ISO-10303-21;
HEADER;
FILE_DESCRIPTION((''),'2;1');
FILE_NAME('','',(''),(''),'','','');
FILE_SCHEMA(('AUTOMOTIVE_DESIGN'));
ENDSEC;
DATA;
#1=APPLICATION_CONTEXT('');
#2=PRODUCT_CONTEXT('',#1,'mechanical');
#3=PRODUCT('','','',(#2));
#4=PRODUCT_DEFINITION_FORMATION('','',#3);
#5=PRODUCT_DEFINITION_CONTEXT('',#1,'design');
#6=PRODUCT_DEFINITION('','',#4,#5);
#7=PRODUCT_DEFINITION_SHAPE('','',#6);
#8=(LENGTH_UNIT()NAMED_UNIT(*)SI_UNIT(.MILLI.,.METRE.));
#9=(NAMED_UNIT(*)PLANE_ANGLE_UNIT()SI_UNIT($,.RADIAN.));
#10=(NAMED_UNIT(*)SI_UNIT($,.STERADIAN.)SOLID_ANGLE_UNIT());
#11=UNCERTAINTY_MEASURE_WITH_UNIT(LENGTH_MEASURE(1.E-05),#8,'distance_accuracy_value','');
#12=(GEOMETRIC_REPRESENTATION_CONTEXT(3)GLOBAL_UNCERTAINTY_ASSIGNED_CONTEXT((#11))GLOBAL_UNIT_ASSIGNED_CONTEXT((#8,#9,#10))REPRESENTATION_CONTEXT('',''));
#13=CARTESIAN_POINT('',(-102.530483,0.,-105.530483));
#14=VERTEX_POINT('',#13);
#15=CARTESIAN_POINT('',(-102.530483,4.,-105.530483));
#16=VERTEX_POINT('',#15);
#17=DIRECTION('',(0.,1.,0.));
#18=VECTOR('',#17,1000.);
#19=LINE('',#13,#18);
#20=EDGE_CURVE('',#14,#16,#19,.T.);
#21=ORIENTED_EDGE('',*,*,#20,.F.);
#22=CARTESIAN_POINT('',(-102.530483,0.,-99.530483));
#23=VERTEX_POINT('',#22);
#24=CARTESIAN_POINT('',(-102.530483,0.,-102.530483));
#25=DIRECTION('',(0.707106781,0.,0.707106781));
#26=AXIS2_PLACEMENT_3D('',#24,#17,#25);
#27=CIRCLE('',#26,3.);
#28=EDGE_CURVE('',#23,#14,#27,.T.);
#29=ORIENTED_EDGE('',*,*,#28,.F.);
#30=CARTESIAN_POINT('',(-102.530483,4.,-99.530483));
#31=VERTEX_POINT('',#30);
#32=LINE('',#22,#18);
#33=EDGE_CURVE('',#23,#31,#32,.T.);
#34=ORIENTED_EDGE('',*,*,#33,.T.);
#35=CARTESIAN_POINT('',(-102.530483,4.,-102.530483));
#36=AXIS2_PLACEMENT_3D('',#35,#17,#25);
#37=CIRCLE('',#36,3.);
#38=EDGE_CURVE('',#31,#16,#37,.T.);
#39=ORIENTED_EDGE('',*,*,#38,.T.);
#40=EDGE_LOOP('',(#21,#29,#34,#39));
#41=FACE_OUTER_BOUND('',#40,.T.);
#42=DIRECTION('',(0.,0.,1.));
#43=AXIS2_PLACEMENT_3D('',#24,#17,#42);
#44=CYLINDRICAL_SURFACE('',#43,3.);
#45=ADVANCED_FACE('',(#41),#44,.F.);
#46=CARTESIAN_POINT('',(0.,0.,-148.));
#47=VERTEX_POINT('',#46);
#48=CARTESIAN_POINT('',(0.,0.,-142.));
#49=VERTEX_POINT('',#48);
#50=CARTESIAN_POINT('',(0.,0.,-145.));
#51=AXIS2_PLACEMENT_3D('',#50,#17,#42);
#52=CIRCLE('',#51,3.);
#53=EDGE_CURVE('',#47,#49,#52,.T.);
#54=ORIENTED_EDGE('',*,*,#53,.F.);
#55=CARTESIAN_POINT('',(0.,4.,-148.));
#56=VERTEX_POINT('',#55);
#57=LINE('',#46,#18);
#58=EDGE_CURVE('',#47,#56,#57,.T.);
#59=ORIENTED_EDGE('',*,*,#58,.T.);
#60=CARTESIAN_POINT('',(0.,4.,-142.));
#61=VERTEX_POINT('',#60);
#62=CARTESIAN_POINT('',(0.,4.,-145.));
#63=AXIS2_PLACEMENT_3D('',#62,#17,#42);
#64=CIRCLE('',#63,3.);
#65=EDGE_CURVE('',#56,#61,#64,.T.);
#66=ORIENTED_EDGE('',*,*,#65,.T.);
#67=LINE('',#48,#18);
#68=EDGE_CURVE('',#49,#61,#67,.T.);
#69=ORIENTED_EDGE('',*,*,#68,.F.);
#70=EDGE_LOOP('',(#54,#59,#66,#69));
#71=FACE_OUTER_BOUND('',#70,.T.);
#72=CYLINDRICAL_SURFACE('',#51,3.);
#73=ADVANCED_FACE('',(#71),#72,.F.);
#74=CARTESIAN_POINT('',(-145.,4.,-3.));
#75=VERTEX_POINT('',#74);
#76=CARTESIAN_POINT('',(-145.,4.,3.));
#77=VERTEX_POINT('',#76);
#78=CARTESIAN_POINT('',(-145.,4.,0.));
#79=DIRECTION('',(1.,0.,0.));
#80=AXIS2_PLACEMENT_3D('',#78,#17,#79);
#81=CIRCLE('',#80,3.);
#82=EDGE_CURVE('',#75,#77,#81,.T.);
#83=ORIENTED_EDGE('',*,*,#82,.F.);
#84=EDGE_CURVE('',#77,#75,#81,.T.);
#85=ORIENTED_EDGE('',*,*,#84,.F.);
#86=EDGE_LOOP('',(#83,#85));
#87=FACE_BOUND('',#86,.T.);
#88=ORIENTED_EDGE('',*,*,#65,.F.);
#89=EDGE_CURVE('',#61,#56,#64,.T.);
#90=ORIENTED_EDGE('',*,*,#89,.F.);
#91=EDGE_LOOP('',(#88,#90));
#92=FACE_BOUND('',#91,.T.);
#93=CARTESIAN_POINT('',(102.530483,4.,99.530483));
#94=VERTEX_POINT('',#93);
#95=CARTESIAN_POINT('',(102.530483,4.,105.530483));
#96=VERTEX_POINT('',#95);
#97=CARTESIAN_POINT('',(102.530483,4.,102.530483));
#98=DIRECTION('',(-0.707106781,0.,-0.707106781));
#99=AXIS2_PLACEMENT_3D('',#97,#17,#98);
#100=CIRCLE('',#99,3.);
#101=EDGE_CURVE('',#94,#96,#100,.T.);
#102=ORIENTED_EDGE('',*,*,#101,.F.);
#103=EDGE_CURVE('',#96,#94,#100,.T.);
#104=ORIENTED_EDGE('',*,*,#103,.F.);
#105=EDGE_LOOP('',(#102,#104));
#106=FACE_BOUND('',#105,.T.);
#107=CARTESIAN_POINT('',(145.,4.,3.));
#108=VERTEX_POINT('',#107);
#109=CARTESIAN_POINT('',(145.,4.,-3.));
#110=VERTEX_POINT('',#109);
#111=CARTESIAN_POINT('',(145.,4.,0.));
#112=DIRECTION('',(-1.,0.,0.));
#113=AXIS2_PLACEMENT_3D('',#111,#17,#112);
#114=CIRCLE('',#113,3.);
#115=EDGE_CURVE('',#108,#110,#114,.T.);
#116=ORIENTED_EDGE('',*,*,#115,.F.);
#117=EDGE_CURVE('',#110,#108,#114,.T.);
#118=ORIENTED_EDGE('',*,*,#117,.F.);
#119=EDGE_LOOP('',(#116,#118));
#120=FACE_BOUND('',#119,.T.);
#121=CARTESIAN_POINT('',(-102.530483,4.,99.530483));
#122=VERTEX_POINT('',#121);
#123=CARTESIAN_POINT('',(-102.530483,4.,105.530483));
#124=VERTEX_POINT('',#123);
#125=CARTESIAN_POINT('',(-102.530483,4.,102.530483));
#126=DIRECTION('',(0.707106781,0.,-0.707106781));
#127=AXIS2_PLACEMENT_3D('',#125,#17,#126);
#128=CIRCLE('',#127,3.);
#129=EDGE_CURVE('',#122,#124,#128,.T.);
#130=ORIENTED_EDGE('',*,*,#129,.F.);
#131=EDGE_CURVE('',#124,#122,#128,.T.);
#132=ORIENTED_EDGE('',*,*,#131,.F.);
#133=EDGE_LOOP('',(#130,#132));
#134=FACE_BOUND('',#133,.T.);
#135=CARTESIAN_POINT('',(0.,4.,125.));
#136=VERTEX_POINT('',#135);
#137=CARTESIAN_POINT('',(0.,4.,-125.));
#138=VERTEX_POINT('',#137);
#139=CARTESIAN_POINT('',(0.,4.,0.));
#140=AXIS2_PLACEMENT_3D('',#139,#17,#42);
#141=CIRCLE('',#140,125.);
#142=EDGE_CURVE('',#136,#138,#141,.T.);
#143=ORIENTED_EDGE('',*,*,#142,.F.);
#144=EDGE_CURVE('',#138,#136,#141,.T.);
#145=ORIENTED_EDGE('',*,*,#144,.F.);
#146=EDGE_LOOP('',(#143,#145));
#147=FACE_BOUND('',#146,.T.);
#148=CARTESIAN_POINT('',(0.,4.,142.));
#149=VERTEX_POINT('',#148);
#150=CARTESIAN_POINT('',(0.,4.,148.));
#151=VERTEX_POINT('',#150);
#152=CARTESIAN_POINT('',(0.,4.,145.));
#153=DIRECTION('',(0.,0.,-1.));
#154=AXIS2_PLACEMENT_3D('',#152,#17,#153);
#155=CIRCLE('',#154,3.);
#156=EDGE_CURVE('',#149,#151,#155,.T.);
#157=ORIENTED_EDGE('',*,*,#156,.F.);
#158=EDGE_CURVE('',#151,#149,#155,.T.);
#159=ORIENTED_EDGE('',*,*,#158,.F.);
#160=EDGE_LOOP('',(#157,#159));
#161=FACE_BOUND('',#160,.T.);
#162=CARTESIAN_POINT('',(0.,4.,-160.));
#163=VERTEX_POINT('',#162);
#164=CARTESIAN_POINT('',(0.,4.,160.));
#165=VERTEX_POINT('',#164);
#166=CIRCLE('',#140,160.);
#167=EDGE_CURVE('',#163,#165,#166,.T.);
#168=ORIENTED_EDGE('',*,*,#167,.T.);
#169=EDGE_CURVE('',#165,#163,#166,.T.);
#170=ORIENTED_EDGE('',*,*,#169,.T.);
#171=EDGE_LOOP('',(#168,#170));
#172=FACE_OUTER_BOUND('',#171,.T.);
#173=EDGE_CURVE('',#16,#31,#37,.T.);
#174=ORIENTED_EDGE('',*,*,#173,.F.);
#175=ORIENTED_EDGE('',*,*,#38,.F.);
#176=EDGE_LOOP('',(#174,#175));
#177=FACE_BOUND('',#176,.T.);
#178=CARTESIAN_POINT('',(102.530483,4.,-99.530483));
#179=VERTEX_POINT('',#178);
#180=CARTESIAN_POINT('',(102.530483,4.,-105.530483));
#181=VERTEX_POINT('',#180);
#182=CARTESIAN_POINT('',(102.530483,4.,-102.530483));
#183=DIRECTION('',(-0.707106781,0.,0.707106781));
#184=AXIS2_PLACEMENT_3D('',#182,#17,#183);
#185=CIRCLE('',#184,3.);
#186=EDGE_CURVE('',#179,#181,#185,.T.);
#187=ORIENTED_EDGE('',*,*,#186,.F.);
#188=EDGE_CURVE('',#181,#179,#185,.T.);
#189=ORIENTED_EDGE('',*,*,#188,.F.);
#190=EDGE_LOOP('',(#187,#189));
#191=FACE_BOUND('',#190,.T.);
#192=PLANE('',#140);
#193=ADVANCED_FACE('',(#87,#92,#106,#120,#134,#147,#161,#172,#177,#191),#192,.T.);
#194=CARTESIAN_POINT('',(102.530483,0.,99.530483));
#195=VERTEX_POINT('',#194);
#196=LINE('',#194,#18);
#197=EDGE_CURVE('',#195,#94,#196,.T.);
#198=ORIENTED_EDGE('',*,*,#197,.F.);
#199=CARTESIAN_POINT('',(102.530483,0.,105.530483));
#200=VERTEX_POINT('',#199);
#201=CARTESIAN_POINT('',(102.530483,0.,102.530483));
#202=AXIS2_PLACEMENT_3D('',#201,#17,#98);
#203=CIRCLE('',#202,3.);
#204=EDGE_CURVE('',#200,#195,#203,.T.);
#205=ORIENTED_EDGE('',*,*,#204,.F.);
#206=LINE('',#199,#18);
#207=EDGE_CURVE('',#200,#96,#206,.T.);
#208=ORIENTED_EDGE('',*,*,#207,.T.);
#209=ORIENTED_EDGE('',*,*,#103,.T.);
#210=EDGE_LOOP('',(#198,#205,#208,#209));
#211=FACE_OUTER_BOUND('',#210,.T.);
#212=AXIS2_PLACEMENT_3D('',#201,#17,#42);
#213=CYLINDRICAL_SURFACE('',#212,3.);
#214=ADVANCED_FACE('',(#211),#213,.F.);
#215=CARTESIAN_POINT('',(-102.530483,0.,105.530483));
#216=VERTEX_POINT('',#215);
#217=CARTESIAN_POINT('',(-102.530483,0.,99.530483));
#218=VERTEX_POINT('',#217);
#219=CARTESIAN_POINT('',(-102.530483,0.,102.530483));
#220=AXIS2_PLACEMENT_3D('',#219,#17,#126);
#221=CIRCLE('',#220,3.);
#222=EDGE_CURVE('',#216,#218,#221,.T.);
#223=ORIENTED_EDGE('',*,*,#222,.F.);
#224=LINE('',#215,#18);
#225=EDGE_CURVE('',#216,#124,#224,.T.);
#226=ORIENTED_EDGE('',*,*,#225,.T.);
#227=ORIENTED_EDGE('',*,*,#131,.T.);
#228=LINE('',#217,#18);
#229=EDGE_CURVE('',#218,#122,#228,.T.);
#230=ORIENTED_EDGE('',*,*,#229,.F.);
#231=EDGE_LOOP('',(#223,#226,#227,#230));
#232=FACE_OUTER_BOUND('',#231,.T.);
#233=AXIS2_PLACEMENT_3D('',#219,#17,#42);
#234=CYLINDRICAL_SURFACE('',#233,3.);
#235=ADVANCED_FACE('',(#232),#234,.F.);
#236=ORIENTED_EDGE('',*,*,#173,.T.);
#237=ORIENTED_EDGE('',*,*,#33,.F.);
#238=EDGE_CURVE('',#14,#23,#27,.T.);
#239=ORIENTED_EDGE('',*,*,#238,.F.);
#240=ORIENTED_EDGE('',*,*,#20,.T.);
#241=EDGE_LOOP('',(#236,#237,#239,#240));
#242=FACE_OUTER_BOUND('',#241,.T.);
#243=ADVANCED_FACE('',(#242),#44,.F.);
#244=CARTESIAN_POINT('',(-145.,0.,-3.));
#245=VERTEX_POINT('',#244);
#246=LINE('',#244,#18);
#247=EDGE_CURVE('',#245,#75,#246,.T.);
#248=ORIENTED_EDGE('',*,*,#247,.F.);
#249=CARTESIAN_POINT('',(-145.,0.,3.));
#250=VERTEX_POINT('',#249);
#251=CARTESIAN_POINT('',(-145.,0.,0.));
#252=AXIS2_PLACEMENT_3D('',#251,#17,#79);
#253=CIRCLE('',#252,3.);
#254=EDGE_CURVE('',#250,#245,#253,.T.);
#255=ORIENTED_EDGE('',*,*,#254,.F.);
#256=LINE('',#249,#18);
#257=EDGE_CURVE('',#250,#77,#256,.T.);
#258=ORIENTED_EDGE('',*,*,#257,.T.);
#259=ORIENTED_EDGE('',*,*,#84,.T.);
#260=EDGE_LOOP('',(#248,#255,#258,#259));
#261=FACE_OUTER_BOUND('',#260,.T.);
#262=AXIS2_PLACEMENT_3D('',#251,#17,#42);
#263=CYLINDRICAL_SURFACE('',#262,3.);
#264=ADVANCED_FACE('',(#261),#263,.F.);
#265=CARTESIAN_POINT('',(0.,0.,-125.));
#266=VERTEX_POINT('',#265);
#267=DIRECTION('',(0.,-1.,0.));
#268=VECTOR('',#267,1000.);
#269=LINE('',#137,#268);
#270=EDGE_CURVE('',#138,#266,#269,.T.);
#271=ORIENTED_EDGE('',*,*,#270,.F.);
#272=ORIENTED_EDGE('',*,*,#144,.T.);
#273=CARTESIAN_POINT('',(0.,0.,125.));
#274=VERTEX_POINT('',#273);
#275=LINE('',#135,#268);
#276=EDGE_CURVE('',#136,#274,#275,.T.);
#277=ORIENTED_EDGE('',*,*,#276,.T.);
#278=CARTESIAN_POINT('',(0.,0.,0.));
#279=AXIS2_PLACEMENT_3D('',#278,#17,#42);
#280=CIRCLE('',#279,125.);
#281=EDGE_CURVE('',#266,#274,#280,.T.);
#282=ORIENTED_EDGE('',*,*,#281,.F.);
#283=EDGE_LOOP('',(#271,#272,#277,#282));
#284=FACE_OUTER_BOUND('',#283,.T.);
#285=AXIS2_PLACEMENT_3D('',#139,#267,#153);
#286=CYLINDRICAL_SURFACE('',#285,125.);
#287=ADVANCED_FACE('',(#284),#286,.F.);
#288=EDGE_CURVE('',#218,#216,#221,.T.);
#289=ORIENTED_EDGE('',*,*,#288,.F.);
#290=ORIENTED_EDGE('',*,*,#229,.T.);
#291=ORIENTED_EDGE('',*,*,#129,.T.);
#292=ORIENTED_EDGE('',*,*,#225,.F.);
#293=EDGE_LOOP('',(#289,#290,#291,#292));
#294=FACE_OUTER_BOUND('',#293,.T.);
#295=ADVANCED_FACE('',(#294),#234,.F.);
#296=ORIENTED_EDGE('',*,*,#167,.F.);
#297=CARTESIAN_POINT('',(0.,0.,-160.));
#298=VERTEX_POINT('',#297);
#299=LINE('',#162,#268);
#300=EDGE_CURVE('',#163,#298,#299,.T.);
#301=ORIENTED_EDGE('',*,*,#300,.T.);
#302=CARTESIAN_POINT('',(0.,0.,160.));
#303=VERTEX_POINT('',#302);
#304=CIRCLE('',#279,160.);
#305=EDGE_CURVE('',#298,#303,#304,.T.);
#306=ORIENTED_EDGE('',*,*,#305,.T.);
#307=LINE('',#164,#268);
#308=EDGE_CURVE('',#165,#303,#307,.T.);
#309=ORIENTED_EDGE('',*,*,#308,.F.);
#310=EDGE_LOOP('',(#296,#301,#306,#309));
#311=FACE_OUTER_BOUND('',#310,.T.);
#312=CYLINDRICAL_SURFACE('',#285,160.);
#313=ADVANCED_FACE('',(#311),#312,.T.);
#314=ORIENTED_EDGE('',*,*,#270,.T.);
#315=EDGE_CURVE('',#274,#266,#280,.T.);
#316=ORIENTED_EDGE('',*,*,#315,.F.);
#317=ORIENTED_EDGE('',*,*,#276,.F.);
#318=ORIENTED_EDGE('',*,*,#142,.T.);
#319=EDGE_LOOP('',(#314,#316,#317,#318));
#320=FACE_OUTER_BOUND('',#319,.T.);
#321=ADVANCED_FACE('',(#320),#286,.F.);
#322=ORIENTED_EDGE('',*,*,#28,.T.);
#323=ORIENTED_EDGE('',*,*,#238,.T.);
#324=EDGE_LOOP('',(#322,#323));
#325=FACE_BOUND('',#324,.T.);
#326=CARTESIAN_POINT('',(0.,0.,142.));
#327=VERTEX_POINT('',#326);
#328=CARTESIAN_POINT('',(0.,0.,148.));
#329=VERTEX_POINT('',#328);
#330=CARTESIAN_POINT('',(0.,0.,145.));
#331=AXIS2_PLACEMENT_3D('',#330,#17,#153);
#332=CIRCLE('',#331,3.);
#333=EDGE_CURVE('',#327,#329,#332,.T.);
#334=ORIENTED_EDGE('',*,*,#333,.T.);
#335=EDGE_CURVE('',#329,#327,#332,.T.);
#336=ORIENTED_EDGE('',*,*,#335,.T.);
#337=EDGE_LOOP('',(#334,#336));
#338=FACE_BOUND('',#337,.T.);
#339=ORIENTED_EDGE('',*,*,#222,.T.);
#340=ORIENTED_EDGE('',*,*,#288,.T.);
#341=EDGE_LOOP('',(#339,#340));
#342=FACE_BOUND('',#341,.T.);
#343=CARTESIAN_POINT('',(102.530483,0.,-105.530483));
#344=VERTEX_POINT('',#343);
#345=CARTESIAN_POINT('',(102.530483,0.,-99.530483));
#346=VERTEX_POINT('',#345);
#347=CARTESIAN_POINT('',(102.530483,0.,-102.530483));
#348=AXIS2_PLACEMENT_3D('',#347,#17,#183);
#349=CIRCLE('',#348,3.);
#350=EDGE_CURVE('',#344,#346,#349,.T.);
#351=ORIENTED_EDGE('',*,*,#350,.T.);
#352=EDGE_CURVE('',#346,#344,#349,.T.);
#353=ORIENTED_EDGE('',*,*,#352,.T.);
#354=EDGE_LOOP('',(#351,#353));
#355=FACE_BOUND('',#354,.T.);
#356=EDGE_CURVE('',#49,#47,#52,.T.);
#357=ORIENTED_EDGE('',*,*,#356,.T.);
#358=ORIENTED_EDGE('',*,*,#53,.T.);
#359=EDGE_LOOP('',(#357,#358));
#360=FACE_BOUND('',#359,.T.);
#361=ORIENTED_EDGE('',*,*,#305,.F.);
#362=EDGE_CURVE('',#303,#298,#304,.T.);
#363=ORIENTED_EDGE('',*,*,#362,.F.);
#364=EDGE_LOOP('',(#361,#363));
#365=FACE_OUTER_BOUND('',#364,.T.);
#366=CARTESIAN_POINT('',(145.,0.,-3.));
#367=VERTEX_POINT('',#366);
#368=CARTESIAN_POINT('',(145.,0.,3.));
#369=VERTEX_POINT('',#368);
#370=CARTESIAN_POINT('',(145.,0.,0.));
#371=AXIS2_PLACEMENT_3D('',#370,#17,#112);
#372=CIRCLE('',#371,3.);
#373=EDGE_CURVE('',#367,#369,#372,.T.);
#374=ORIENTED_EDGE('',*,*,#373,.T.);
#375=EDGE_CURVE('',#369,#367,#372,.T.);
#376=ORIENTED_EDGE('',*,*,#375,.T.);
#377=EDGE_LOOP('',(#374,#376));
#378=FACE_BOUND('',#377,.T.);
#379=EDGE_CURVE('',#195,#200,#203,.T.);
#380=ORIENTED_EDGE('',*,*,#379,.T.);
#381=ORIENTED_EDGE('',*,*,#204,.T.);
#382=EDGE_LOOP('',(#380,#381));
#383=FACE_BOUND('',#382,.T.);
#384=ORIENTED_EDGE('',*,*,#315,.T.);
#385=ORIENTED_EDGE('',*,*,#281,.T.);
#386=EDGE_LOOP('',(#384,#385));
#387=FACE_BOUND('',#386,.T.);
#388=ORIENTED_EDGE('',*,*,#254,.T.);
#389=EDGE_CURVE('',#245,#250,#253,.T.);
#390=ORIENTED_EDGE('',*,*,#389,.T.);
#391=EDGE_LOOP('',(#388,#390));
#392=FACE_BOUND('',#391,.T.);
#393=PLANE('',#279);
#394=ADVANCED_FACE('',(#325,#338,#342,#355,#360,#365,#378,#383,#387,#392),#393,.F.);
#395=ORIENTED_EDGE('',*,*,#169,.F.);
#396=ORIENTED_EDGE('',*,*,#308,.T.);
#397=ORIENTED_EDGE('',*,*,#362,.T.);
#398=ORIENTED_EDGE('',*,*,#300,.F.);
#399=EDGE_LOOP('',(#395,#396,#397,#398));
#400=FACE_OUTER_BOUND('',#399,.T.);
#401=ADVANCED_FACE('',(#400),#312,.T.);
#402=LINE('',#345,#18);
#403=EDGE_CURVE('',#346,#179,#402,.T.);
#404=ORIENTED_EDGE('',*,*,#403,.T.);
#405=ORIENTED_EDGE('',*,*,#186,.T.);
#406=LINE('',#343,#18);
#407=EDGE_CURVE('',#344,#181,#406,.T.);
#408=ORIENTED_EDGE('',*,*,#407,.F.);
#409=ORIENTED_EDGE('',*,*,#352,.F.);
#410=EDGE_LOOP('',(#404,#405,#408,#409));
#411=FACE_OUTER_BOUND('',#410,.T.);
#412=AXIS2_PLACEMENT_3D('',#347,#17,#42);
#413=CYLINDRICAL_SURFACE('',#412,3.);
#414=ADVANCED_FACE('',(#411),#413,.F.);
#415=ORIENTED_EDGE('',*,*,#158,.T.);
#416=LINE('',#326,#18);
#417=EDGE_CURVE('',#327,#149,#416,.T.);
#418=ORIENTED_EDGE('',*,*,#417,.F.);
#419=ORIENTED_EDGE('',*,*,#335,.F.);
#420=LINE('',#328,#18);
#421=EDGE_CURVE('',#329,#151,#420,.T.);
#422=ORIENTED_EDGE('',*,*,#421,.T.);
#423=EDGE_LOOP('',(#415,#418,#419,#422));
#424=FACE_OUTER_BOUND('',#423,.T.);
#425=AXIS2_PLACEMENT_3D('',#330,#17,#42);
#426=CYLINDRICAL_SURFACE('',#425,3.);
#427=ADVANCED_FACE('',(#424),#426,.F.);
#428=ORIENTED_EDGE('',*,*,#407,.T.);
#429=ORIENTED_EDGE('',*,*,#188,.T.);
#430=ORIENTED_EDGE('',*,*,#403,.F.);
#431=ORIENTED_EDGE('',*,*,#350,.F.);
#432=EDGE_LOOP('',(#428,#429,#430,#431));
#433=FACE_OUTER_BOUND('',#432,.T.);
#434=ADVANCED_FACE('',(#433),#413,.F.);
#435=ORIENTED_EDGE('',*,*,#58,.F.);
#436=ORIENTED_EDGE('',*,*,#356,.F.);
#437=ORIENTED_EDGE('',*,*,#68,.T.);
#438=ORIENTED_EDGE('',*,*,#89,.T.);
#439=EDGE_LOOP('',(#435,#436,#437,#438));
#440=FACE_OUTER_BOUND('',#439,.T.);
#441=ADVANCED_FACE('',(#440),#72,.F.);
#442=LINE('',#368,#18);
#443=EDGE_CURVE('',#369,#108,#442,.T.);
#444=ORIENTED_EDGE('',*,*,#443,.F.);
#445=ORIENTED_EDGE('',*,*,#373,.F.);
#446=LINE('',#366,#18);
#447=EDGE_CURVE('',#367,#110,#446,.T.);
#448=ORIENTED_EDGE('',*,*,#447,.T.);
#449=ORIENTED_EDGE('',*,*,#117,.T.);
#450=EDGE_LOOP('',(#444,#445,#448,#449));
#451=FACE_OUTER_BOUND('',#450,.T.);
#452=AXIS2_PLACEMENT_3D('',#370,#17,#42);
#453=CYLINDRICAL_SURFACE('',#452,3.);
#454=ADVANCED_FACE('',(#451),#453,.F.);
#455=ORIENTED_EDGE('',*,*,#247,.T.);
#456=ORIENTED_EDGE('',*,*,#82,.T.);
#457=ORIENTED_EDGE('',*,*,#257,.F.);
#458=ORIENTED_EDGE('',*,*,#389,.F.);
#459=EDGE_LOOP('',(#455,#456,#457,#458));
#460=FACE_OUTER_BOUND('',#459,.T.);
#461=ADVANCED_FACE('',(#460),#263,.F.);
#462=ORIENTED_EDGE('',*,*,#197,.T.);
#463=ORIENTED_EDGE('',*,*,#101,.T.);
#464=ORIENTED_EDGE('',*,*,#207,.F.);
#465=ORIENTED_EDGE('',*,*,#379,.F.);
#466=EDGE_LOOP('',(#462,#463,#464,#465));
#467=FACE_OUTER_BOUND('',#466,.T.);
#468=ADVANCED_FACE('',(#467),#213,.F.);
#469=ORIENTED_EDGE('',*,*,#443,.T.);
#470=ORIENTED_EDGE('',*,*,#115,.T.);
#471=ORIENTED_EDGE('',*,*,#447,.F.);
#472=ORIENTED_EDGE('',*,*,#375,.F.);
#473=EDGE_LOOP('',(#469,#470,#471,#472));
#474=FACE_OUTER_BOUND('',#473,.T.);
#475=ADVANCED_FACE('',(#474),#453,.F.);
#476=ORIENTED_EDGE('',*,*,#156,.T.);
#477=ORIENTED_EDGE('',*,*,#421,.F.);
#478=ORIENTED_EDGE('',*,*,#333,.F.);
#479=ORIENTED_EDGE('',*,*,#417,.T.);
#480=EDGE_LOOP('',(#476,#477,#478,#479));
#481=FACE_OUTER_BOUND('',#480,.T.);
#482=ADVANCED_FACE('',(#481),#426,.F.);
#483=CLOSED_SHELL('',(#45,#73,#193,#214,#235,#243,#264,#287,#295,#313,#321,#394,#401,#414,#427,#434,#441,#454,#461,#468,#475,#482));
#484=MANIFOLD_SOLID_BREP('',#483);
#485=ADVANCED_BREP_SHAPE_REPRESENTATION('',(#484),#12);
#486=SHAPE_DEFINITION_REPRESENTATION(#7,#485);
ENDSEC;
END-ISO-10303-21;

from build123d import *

# Parameters (mm, degrees)
SKETCH_1_R               = 160
SKETCH_1_R_2             = 125
EXTRUDE_1_DEPTH          = 4
SKETCH_2_R               = 3
CUT_EXTRUDE_1_DEPTH      = 227.309522557
PATTERN_CIRCULAR_1_COUNT = 8


with BuildPart() as part:
    # 草图1 → 凸台-拉伸1 (new body)
    with BuildSketch(Plane(origin=(0, 0, 0), x_dir=(1, 0, 0), z_dir=(0, 1, 0))):
        with Locations(Location((0, 0, 0), (0, 0, 270))):
            Circle(SKETCH_1_R)
        with Locations(Location((0, 0, 0), (0, 0, 270))):
            Circle(SKETCH_1_R_2, mode=Mode.SUBTRACT)
    extrude(amount=EXTRUDE_1_DEPTH)

    # 草图2 → 切除-拉伸1 (cut, through all)
    with BuildSketch(Plane(origin=(0, 4, 0), x_dir=(1, 0, 0), z_dir=(0, 1, 0))):
        with Locations(Location((0, 145, 0), (0, 0, 270))):
            Circle(SKETCH_2_R)
    cut_extrude_1 = extrude(amount=-CUT_EXTRUDE_1_DEPTH, mode=Mode.SUBTRACT)

    # 阵列(圆周)1: 切除-拉伸1 ×8 about axis
    pattern_circular_1_axis = Axis((0, 0, 0), (0, 1, 0))
    for i in range(1, PATTERN_CIRCULAR_1_COUNT):
        add(cut_extrude_1.rotate(pattern_circular_1_axis, i * 360 / PATTERN_CIRCULAR_1_COUNT), mode=Mode.SUBTRACT)


solid = part.part
